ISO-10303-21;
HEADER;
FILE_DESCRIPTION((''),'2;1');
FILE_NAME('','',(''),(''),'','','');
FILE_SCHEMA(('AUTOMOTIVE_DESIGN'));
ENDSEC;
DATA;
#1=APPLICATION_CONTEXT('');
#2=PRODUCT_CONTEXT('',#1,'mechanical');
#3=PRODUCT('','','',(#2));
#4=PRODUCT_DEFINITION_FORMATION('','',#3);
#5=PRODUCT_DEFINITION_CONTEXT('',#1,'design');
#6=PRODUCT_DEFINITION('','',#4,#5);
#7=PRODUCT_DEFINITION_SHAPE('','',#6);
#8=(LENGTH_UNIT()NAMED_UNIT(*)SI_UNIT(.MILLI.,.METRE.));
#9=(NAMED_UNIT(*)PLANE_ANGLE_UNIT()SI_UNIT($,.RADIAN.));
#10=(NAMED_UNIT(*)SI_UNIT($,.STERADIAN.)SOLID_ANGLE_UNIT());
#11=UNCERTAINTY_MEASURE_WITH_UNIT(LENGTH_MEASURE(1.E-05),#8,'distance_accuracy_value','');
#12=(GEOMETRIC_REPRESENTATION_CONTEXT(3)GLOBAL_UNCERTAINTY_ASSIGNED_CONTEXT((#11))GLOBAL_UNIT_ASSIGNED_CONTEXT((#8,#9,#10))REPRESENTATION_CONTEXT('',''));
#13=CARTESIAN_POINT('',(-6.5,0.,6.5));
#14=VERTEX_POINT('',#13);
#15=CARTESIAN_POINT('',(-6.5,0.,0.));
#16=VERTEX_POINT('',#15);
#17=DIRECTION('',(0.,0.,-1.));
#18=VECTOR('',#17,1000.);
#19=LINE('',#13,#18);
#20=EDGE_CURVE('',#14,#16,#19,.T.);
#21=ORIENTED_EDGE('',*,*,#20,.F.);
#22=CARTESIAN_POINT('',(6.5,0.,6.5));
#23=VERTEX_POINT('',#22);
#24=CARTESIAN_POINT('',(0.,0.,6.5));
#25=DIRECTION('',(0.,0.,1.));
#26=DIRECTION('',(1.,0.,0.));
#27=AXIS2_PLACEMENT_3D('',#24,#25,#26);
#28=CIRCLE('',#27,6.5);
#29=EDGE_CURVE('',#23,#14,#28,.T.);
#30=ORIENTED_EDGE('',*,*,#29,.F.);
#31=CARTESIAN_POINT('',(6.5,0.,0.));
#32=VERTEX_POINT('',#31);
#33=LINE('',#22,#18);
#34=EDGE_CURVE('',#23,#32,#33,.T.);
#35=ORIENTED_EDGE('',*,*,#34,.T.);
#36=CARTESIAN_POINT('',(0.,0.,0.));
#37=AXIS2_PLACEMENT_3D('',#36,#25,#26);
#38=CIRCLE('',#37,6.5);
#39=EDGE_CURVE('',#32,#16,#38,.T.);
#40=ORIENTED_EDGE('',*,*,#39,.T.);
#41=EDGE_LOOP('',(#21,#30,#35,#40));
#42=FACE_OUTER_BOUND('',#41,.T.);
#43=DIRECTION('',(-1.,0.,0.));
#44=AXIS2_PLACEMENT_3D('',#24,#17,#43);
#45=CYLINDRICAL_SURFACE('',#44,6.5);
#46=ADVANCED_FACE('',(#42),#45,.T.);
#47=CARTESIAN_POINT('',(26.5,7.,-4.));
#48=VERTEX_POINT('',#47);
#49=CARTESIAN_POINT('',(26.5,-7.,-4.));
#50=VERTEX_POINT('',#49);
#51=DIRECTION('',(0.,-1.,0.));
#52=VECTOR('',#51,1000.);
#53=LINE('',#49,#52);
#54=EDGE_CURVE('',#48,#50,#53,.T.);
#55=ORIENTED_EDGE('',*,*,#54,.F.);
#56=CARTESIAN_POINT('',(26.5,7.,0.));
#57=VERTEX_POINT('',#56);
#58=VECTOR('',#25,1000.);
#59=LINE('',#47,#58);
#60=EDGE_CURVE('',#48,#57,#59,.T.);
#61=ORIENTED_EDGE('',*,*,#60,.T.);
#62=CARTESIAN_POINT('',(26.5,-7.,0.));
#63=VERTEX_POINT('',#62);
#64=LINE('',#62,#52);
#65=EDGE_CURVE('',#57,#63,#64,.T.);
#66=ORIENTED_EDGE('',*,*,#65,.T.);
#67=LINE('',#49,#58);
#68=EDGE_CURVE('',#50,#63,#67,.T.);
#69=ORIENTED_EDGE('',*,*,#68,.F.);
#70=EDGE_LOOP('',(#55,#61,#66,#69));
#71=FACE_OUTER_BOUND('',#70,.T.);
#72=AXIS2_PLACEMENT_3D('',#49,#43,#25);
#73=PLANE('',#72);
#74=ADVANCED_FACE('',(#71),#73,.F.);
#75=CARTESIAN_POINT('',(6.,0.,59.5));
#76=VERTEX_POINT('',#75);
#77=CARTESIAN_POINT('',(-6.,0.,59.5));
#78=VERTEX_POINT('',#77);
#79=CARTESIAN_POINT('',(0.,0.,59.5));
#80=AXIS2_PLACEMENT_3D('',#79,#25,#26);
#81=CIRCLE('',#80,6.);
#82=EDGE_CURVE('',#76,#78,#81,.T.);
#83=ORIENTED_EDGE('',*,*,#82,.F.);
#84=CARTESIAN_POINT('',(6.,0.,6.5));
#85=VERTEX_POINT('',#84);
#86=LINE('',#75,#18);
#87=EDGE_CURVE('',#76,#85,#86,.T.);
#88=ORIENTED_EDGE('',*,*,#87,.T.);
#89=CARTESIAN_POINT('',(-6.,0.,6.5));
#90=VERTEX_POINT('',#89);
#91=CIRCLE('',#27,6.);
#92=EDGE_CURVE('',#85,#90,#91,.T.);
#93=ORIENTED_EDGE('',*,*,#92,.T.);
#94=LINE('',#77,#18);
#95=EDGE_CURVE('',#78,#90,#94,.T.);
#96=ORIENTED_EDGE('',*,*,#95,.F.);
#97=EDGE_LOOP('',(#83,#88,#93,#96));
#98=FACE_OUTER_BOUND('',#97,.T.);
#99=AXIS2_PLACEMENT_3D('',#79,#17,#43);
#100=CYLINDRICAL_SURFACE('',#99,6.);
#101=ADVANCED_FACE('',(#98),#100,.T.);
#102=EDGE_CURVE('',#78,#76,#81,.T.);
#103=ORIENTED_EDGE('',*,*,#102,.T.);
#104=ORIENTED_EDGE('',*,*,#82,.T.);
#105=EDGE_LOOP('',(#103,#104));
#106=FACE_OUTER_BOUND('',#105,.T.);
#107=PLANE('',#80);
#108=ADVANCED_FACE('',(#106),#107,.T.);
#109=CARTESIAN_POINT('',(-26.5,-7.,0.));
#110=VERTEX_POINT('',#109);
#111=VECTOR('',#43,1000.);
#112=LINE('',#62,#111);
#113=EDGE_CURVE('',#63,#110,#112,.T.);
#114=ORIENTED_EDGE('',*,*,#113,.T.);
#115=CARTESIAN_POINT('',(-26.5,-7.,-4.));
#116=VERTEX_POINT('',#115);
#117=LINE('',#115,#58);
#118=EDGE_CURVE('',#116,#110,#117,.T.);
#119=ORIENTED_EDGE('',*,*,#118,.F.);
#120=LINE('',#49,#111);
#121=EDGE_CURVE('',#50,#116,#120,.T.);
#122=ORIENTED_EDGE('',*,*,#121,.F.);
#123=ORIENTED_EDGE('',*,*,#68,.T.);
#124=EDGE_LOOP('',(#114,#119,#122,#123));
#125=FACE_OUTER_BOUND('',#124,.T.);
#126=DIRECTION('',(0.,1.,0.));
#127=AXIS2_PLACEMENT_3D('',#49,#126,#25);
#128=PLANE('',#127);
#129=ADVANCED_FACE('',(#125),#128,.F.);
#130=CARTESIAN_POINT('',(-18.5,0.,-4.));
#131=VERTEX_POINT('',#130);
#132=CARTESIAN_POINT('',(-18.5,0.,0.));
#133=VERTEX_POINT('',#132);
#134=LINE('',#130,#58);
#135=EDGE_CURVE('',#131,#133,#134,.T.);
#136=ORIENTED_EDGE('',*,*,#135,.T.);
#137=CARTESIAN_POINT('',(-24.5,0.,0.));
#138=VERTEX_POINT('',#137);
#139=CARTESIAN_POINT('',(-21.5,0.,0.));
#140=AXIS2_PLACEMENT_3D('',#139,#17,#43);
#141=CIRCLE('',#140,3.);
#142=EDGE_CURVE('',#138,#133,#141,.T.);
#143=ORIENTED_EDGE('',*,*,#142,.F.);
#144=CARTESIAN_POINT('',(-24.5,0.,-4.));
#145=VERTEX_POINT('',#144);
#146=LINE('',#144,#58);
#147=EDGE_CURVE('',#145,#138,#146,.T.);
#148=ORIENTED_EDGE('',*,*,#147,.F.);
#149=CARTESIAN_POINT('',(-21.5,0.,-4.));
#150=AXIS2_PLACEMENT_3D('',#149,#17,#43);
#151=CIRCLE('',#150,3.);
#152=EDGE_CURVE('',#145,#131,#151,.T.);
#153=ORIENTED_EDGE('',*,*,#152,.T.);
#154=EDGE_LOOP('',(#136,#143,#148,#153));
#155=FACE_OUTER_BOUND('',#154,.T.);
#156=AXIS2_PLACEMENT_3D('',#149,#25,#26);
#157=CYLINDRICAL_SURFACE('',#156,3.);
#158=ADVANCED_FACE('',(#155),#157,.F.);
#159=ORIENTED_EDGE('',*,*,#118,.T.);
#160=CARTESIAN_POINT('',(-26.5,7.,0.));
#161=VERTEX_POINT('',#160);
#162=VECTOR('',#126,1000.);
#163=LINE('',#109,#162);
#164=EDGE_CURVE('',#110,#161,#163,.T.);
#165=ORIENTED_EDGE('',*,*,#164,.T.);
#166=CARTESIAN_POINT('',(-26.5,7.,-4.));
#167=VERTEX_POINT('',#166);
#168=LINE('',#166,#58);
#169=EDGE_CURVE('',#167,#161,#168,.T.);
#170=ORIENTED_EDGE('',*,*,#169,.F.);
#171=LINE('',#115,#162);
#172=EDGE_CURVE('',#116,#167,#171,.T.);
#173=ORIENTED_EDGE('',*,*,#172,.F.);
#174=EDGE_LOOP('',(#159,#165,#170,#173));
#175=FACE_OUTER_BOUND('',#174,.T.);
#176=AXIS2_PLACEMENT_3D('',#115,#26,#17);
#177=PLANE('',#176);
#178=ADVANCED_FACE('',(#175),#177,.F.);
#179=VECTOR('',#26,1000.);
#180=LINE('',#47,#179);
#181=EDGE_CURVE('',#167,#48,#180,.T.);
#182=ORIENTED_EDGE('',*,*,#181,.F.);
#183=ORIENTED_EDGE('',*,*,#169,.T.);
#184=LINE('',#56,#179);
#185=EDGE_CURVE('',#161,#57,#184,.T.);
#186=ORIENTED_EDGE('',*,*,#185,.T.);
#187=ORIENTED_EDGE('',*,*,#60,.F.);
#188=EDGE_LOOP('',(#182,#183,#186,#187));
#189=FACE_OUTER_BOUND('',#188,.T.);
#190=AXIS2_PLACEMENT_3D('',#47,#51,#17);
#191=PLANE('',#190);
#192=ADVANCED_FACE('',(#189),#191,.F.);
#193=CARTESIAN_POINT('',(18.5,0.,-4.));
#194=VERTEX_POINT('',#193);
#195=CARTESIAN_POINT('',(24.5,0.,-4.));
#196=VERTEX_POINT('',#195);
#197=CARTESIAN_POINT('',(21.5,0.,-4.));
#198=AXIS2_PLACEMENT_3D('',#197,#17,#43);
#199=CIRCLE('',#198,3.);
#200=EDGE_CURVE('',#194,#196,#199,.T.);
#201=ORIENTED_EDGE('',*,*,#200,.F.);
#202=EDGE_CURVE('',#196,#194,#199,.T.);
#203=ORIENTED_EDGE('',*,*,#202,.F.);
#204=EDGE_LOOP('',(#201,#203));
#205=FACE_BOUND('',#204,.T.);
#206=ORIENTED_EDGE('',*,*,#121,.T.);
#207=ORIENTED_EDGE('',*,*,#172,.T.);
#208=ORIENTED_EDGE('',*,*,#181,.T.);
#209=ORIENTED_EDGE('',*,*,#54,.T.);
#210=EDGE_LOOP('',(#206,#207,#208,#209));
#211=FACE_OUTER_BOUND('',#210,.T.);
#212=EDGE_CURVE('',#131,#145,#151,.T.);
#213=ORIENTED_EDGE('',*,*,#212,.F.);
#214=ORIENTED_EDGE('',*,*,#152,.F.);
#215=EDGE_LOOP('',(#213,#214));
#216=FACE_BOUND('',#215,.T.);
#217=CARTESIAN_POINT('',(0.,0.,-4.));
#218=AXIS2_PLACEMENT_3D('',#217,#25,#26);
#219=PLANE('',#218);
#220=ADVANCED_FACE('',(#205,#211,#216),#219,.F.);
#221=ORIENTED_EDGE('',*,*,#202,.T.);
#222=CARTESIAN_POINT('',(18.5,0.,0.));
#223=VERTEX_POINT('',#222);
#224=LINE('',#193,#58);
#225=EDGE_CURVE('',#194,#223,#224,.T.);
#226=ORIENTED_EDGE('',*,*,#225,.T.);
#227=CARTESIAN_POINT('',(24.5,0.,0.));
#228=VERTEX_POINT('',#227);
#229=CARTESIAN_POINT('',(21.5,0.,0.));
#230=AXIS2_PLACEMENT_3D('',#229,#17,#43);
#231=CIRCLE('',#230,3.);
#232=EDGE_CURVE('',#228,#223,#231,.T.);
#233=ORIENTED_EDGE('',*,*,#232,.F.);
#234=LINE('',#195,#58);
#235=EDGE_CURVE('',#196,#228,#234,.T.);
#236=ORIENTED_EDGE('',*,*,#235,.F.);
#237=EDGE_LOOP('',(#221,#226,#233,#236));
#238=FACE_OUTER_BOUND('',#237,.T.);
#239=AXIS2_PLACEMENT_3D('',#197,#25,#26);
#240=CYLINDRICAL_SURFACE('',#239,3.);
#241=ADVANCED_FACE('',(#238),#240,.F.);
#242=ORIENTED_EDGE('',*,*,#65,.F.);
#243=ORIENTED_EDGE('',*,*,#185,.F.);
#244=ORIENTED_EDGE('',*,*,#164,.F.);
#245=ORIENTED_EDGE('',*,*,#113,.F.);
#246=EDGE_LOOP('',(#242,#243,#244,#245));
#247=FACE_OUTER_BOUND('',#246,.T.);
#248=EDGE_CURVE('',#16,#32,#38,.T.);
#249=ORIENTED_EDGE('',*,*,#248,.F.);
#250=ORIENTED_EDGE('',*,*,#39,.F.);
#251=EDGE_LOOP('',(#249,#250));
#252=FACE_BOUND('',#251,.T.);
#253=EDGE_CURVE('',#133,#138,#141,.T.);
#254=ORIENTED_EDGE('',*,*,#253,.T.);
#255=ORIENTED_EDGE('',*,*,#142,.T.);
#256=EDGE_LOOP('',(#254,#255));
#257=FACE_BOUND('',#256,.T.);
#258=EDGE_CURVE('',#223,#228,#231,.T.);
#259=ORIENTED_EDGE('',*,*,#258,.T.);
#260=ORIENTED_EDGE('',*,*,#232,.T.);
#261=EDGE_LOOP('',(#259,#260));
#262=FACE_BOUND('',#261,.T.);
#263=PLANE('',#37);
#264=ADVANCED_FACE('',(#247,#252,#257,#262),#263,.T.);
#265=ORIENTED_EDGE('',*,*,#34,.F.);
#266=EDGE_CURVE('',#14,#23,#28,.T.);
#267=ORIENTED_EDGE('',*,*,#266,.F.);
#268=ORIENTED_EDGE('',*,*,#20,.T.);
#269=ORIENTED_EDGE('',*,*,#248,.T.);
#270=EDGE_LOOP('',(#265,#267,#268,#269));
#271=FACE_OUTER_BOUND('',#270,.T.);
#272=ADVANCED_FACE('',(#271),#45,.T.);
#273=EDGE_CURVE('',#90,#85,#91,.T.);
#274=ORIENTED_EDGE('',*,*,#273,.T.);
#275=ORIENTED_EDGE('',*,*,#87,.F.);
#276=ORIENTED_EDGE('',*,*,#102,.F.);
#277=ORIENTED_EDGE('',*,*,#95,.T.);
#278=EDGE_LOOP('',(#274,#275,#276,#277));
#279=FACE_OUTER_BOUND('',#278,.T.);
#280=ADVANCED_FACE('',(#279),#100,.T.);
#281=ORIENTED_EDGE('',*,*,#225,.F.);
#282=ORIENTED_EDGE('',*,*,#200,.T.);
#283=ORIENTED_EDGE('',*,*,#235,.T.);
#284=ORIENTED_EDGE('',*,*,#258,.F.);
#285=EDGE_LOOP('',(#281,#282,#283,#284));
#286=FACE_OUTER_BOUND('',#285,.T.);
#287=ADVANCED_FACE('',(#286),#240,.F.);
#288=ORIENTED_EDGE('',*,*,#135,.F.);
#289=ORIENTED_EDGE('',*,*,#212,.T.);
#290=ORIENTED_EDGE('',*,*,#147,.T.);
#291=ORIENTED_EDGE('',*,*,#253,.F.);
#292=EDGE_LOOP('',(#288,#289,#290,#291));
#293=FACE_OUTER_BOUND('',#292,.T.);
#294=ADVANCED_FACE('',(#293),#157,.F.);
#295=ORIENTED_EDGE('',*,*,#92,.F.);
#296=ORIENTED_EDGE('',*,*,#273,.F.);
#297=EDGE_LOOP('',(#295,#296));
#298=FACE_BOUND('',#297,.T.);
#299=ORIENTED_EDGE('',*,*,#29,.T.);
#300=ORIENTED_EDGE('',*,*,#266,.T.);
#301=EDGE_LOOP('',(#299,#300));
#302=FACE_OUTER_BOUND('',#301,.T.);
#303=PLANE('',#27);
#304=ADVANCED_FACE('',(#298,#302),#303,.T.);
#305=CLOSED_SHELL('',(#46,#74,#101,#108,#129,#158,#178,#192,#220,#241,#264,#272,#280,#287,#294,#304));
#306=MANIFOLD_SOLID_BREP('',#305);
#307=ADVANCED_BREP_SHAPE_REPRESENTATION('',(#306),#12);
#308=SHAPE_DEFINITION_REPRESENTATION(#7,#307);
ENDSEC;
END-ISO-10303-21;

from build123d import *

# Parameters (mm, degrees)
SKETCH_1_R      = 6
EXTRUDE_1_DEPTH = 59.5
SKETCH_2_W      = 53
SKETCH_2_H      = 14
SKETCH_2_R      = 3
EXTRUDE_2_DEPTH = 4
SKETCH_3_R      = 6.5
EXTRUDE_3_DEPTH = 6.5


with BuildPart() as part:
    # 草图1 → 凸台-拉伸1 (new body)
    with BuildSketch(Plane.XY):
        with Locations(Location((0, 0, 0), (0, 0, 180))):
            Circle(SKETCH_1_R)
    extrude(amount=EXTRUDE_1_DEPTH)

    # 草图2 → 凸台-拉伸2 (add)
    with BuildSketch(Plane(origin=(0, 0, 0), x_dir=(-1, 0, 0), z_dir=(0, 0, -1))):
        Rectangle(SKETCH_2_W, SKETCH_2_H)
        with Locations((-21.5, 0)):
            Circle(SKETCH_2_R, mode=Mode.SUBTRACT)
        with Locations((21.5, 0)):
            Circle(SKETCH_2_R, mode=Mode.SUBTRACT)
    extrude(amount=EXTRUDE_2_DEPTH)

    # 草图3 → 凸台-拉伸3 (add)
    with BuildSketch(Plane.XY):
        with Locations(Location((0, 0, 0), (0, 0, 180))):
            Circle(SKETCH_3_R)
    extrude(amount=EXTRUDE_3_DEPTH)


solid = part.part
